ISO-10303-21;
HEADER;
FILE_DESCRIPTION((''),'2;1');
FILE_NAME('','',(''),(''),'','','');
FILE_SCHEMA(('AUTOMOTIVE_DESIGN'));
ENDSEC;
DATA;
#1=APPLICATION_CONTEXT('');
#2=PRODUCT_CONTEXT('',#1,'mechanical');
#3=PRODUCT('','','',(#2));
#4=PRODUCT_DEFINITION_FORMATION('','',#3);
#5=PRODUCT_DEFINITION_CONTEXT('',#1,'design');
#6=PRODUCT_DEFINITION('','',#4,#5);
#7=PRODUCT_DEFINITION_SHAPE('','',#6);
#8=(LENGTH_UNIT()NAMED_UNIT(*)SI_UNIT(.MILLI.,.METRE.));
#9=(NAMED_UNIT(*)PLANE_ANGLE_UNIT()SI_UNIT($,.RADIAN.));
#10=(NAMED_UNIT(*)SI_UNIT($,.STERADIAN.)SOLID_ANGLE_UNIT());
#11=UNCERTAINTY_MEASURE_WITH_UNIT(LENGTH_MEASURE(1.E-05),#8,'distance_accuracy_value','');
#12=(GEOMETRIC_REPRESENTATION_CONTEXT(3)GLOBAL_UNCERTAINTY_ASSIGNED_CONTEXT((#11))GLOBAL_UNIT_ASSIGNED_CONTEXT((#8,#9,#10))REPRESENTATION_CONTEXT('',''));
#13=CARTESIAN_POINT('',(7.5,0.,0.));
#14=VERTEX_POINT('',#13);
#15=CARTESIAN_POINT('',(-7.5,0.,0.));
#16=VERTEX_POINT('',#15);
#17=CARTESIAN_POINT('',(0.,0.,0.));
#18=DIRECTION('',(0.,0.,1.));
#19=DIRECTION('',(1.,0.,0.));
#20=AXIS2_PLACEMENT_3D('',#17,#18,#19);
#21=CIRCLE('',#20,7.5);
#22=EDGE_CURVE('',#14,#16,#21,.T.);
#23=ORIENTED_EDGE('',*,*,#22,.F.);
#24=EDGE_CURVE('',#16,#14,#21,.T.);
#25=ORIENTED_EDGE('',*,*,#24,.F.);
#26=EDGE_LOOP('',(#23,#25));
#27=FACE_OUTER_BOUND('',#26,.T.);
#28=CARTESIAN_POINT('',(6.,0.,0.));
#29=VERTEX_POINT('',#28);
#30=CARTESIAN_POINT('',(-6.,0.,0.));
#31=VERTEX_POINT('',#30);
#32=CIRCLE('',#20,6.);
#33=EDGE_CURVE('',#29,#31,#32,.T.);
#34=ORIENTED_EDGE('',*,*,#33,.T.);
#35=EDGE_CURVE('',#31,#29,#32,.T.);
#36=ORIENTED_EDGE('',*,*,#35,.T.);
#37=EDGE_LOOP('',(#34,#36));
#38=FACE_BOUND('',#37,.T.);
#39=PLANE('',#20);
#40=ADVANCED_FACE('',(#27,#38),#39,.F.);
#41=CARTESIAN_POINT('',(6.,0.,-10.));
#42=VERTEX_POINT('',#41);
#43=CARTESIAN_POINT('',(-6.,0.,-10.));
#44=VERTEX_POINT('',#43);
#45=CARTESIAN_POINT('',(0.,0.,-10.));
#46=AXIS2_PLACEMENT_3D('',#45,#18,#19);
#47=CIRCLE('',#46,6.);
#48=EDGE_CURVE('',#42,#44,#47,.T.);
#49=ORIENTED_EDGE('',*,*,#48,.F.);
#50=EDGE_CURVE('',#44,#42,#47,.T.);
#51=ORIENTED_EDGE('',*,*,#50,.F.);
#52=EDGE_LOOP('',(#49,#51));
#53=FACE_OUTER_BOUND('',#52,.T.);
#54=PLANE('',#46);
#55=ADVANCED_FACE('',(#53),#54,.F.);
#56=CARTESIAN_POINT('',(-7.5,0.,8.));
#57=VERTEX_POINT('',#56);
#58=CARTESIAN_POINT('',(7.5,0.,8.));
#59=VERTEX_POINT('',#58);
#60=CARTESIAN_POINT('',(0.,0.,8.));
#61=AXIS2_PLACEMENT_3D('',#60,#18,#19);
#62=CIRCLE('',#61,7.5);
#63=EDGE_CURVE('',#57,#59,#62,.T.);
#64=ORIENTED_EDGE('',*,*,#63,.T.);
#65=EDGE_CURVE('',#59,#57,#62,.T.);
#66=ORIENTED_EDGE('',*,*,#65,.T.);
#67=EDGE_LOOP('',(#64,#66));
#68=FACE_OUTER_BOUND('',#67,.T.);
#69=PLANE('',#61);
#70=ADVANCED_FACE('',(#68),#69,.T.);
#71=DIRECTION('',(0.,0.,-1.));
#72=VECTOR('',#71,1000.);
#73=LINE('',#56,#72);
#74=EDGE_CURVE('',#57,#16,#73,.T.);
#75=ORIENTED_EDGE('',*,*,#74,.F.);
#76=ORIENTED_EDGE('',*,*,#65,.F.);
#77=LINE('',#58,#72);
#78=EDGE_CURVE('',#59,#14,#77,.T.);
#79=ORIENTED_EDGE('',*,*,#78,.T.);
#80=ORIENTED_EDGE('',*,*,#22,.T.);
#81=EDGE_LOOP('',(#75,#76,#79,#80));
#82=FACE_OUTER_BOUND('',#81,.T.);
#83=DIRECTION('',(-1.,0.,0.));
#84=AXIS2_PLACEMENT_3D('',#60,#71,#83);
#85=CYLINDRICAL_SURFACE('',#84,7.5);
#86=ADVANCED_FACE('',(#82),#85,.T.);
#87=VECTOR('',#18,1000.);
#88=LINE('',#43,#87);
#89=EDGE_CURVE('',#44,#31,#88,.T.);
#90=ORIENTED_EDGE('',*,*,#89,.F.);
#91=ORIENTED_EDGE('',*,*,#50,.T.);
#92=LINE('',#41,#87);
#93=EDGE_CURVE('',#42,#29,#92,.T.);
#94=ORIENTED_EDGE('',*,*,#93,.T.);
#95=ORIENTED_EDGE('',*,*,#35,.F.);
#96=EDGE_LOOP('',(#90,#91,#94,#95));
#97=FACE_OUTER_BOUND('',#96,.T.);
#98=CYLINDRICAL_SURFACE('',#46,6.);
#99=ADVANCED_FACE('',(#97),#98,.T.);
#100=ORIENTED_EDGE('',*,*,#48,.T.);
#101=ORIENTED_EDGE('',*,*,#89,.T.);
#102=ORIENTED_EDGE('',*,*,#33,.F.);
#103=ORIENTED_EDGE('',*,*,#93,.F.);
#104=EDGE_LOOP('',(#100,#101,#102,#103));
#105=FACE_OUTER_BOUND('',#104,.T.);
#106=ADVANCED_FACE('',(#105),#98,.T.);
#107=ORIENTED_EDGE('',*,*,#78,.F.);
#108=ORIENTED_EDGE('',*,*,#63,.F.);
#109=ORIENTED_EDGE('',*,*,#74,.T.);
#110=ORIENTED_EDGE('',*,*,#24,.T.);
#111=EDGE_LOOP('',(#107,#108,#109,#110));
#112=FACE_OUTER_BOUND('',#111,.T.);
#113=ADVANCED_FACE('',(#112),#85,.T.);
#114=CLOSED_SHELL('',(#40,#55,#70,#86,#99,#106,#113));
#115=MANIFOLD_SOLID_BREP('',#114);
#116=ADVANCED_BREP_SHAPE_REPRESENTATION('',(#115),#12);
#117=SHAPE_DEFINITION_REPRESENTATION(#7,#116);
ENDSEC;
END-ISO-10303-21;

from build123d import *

# Parameters (mm, degrees)
SKETCH_1_R      = 6
EXTRUDE_1_DEPTH = 10
SKETCH_2_R      = 7.5
EXTRUDE_2_DEPTH = 8


with BuildPart() as part:
    # 草图1 → 凸台-拉伸1 (new body)
    with BuildSketch(Plane.XY):
        Circle(SKETCH_1_R)
    extrude(amount=-EXTRUDE_1_DEPTH)

    # 草图2 → 凸台-拉伸2 (add)
    with BuildSketch(Plane.XY):
        Circle(SKETCH_2_R)
    extrude(amount=EXTRUDE_2_DEPTH)


solid = part.part
